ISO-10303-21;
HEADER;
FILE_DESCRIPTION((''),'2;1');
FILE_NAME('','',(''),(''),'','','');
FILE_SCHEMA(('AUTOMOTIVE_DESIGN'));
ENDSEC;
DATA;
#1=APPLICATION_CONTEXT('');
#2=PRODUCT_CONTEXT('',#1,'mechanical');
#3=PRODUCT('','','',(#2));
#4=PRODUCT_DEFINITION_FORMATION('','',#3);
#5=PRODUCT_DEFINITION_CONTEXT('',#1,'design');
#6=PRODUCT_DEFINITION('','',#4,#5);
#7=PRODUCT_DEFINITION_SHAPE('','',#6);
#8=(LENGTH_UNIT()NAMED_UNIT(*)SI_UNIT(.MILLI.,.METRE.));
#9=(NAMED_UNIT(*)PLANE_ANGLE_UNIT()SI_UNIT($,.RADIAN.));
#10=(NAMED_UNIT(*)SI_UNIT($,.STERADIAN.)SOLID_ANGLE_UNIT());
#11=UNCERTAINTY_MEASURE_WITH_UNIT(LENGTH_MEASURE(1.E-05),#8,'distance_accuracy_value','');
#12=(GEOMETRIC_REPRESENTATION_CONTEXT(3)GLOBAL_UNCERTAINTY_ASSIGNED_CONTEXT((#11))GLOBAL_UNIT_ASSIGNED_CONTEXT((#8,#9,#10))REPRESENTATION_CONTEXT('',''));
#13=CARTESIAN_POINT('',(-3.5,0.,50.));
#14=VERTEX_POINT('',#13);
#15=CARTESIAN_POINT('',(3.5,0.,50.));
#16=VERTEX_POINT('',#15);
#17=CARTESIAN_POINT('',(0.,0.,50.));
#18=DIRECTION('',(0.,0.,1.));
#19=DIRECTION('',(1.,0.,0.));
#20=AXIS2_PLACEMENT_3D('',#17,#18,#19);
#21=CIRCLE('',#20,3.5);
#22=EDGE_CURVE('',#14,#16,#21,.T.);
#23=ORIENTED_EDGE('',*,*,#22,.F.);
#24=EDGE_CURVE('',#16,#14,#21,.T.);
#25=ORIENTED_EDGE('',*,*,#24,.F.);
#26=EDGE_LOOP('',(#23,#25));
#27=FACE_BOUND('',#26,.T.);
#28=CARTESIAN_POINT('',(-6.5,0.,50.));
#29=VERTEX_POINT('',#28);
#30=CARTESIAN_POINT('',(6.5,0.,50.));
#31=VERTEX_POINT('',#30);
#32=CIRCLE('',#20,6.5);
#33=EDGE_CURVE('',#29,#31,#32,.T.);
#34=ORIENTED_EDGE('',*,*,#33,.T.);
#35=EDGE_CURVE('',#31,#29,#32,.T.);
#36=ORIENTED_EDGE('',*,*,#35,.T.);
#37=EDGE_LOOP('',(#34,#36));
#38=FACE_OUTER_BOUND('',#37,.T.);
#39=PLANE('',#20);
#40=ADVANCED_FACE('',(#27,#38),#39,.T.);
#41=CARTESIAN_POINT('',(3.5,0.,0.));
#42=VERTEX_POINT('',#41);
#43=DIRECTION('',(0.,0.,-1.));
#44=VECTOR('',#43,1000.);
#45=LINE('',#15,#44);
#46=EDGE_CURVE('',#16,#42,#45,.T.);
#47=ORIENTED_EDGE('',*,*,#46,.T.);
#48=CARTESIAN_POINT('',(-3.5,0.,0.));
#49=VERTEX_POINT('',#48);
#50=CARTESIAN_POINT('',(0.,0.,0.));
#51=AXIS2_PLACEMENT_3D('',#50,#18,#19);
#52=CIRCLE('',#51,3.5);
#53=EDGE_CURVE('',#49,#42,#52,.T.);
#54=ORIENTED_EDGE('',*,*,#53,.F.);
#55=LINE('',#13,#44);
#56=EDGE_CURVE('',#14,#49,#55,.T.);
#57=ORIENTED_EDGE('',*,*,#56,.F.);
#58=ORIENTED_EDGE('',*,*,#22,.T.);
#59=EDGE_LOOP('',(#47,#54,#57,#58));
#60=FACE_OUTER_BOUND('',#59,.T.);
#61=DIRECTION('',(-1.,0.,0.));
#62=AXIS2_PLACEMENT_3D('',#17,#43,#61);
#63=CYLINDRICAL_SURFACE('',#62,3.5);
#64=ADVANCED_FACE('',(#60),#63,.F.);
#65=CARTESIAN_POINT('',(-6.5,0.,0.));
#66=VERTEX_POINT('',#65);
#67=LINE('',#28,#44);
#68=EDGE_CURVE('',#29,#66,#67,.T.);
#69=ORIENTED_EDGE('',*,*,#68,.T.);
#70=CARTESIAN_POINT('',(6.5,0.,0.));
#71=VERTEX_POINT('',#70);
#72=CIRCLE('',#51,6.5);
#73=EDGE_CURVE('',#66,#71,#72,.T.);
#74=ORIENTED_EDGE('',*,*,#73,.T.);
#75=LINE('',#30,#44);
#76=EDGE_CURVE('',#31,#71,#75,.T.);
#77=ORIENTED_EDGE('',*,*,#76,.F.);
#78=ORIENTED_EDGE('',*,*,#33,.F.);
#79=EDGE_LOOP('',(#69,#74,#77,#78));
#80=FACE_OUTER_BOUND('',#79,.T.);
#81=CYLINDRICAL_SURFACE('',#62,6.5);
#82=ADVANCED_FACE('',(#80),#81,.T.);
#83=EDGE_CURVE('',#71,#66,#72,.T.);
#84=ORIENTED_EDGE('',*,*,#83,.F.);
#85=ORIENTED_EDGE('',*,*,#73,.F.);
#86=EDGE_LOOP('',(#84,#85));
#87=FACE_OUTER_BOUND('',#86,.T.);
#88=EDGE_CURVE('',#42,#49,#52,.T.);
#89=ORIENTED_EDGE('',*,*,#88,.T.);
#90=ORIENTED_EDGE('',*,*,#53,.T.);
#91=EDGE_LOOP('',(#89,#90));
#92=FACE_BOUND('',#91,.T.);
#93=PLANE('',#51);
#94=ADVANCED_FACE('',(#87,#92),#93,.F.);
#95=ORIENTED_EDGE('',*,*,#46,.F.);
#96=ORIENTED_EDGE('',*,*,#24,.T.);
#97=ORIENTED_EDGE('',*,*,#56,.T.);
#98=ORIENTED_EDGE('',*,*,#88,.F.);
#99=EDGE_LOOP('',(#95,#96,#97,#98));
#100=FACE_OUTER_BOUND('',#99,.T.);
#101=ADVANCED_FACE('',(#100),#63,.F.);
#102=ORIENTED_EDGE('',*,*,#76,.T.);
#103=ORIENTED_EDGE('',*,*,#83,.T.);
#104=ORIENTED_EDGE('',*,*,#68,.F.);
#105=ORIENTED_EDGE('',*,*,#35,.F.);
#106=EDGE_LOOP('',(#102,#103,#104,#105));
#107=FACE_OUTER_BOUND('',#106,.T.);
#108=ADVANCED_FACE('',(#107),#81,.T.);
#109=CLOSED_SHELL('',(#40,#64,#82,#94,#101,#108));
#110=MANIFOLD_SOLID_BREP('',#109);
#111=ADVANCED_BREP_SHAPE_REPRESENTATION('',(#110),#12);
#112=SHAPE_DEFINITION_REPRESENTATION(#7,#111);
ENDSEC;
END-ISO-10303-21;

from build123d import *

# Parameters (mm, degrees)
SKETCH_1_R      = 6.5
SKETCH_1_R_2    = 3.5
EXTRUDE_1_DEPTH = 50


with BuildPart() as part:
    # 草图1 → 凸台-拉伸1 (new body)
    with BuildSketch(Plane.XY):
        Circle(SKETCH_1_R)
        Circle(SKETCH_1_R_2, mode=Mode.SUBTRACT)
    extrude(amount=EXTRUDE_1_DEPTH)


solid = part.part
